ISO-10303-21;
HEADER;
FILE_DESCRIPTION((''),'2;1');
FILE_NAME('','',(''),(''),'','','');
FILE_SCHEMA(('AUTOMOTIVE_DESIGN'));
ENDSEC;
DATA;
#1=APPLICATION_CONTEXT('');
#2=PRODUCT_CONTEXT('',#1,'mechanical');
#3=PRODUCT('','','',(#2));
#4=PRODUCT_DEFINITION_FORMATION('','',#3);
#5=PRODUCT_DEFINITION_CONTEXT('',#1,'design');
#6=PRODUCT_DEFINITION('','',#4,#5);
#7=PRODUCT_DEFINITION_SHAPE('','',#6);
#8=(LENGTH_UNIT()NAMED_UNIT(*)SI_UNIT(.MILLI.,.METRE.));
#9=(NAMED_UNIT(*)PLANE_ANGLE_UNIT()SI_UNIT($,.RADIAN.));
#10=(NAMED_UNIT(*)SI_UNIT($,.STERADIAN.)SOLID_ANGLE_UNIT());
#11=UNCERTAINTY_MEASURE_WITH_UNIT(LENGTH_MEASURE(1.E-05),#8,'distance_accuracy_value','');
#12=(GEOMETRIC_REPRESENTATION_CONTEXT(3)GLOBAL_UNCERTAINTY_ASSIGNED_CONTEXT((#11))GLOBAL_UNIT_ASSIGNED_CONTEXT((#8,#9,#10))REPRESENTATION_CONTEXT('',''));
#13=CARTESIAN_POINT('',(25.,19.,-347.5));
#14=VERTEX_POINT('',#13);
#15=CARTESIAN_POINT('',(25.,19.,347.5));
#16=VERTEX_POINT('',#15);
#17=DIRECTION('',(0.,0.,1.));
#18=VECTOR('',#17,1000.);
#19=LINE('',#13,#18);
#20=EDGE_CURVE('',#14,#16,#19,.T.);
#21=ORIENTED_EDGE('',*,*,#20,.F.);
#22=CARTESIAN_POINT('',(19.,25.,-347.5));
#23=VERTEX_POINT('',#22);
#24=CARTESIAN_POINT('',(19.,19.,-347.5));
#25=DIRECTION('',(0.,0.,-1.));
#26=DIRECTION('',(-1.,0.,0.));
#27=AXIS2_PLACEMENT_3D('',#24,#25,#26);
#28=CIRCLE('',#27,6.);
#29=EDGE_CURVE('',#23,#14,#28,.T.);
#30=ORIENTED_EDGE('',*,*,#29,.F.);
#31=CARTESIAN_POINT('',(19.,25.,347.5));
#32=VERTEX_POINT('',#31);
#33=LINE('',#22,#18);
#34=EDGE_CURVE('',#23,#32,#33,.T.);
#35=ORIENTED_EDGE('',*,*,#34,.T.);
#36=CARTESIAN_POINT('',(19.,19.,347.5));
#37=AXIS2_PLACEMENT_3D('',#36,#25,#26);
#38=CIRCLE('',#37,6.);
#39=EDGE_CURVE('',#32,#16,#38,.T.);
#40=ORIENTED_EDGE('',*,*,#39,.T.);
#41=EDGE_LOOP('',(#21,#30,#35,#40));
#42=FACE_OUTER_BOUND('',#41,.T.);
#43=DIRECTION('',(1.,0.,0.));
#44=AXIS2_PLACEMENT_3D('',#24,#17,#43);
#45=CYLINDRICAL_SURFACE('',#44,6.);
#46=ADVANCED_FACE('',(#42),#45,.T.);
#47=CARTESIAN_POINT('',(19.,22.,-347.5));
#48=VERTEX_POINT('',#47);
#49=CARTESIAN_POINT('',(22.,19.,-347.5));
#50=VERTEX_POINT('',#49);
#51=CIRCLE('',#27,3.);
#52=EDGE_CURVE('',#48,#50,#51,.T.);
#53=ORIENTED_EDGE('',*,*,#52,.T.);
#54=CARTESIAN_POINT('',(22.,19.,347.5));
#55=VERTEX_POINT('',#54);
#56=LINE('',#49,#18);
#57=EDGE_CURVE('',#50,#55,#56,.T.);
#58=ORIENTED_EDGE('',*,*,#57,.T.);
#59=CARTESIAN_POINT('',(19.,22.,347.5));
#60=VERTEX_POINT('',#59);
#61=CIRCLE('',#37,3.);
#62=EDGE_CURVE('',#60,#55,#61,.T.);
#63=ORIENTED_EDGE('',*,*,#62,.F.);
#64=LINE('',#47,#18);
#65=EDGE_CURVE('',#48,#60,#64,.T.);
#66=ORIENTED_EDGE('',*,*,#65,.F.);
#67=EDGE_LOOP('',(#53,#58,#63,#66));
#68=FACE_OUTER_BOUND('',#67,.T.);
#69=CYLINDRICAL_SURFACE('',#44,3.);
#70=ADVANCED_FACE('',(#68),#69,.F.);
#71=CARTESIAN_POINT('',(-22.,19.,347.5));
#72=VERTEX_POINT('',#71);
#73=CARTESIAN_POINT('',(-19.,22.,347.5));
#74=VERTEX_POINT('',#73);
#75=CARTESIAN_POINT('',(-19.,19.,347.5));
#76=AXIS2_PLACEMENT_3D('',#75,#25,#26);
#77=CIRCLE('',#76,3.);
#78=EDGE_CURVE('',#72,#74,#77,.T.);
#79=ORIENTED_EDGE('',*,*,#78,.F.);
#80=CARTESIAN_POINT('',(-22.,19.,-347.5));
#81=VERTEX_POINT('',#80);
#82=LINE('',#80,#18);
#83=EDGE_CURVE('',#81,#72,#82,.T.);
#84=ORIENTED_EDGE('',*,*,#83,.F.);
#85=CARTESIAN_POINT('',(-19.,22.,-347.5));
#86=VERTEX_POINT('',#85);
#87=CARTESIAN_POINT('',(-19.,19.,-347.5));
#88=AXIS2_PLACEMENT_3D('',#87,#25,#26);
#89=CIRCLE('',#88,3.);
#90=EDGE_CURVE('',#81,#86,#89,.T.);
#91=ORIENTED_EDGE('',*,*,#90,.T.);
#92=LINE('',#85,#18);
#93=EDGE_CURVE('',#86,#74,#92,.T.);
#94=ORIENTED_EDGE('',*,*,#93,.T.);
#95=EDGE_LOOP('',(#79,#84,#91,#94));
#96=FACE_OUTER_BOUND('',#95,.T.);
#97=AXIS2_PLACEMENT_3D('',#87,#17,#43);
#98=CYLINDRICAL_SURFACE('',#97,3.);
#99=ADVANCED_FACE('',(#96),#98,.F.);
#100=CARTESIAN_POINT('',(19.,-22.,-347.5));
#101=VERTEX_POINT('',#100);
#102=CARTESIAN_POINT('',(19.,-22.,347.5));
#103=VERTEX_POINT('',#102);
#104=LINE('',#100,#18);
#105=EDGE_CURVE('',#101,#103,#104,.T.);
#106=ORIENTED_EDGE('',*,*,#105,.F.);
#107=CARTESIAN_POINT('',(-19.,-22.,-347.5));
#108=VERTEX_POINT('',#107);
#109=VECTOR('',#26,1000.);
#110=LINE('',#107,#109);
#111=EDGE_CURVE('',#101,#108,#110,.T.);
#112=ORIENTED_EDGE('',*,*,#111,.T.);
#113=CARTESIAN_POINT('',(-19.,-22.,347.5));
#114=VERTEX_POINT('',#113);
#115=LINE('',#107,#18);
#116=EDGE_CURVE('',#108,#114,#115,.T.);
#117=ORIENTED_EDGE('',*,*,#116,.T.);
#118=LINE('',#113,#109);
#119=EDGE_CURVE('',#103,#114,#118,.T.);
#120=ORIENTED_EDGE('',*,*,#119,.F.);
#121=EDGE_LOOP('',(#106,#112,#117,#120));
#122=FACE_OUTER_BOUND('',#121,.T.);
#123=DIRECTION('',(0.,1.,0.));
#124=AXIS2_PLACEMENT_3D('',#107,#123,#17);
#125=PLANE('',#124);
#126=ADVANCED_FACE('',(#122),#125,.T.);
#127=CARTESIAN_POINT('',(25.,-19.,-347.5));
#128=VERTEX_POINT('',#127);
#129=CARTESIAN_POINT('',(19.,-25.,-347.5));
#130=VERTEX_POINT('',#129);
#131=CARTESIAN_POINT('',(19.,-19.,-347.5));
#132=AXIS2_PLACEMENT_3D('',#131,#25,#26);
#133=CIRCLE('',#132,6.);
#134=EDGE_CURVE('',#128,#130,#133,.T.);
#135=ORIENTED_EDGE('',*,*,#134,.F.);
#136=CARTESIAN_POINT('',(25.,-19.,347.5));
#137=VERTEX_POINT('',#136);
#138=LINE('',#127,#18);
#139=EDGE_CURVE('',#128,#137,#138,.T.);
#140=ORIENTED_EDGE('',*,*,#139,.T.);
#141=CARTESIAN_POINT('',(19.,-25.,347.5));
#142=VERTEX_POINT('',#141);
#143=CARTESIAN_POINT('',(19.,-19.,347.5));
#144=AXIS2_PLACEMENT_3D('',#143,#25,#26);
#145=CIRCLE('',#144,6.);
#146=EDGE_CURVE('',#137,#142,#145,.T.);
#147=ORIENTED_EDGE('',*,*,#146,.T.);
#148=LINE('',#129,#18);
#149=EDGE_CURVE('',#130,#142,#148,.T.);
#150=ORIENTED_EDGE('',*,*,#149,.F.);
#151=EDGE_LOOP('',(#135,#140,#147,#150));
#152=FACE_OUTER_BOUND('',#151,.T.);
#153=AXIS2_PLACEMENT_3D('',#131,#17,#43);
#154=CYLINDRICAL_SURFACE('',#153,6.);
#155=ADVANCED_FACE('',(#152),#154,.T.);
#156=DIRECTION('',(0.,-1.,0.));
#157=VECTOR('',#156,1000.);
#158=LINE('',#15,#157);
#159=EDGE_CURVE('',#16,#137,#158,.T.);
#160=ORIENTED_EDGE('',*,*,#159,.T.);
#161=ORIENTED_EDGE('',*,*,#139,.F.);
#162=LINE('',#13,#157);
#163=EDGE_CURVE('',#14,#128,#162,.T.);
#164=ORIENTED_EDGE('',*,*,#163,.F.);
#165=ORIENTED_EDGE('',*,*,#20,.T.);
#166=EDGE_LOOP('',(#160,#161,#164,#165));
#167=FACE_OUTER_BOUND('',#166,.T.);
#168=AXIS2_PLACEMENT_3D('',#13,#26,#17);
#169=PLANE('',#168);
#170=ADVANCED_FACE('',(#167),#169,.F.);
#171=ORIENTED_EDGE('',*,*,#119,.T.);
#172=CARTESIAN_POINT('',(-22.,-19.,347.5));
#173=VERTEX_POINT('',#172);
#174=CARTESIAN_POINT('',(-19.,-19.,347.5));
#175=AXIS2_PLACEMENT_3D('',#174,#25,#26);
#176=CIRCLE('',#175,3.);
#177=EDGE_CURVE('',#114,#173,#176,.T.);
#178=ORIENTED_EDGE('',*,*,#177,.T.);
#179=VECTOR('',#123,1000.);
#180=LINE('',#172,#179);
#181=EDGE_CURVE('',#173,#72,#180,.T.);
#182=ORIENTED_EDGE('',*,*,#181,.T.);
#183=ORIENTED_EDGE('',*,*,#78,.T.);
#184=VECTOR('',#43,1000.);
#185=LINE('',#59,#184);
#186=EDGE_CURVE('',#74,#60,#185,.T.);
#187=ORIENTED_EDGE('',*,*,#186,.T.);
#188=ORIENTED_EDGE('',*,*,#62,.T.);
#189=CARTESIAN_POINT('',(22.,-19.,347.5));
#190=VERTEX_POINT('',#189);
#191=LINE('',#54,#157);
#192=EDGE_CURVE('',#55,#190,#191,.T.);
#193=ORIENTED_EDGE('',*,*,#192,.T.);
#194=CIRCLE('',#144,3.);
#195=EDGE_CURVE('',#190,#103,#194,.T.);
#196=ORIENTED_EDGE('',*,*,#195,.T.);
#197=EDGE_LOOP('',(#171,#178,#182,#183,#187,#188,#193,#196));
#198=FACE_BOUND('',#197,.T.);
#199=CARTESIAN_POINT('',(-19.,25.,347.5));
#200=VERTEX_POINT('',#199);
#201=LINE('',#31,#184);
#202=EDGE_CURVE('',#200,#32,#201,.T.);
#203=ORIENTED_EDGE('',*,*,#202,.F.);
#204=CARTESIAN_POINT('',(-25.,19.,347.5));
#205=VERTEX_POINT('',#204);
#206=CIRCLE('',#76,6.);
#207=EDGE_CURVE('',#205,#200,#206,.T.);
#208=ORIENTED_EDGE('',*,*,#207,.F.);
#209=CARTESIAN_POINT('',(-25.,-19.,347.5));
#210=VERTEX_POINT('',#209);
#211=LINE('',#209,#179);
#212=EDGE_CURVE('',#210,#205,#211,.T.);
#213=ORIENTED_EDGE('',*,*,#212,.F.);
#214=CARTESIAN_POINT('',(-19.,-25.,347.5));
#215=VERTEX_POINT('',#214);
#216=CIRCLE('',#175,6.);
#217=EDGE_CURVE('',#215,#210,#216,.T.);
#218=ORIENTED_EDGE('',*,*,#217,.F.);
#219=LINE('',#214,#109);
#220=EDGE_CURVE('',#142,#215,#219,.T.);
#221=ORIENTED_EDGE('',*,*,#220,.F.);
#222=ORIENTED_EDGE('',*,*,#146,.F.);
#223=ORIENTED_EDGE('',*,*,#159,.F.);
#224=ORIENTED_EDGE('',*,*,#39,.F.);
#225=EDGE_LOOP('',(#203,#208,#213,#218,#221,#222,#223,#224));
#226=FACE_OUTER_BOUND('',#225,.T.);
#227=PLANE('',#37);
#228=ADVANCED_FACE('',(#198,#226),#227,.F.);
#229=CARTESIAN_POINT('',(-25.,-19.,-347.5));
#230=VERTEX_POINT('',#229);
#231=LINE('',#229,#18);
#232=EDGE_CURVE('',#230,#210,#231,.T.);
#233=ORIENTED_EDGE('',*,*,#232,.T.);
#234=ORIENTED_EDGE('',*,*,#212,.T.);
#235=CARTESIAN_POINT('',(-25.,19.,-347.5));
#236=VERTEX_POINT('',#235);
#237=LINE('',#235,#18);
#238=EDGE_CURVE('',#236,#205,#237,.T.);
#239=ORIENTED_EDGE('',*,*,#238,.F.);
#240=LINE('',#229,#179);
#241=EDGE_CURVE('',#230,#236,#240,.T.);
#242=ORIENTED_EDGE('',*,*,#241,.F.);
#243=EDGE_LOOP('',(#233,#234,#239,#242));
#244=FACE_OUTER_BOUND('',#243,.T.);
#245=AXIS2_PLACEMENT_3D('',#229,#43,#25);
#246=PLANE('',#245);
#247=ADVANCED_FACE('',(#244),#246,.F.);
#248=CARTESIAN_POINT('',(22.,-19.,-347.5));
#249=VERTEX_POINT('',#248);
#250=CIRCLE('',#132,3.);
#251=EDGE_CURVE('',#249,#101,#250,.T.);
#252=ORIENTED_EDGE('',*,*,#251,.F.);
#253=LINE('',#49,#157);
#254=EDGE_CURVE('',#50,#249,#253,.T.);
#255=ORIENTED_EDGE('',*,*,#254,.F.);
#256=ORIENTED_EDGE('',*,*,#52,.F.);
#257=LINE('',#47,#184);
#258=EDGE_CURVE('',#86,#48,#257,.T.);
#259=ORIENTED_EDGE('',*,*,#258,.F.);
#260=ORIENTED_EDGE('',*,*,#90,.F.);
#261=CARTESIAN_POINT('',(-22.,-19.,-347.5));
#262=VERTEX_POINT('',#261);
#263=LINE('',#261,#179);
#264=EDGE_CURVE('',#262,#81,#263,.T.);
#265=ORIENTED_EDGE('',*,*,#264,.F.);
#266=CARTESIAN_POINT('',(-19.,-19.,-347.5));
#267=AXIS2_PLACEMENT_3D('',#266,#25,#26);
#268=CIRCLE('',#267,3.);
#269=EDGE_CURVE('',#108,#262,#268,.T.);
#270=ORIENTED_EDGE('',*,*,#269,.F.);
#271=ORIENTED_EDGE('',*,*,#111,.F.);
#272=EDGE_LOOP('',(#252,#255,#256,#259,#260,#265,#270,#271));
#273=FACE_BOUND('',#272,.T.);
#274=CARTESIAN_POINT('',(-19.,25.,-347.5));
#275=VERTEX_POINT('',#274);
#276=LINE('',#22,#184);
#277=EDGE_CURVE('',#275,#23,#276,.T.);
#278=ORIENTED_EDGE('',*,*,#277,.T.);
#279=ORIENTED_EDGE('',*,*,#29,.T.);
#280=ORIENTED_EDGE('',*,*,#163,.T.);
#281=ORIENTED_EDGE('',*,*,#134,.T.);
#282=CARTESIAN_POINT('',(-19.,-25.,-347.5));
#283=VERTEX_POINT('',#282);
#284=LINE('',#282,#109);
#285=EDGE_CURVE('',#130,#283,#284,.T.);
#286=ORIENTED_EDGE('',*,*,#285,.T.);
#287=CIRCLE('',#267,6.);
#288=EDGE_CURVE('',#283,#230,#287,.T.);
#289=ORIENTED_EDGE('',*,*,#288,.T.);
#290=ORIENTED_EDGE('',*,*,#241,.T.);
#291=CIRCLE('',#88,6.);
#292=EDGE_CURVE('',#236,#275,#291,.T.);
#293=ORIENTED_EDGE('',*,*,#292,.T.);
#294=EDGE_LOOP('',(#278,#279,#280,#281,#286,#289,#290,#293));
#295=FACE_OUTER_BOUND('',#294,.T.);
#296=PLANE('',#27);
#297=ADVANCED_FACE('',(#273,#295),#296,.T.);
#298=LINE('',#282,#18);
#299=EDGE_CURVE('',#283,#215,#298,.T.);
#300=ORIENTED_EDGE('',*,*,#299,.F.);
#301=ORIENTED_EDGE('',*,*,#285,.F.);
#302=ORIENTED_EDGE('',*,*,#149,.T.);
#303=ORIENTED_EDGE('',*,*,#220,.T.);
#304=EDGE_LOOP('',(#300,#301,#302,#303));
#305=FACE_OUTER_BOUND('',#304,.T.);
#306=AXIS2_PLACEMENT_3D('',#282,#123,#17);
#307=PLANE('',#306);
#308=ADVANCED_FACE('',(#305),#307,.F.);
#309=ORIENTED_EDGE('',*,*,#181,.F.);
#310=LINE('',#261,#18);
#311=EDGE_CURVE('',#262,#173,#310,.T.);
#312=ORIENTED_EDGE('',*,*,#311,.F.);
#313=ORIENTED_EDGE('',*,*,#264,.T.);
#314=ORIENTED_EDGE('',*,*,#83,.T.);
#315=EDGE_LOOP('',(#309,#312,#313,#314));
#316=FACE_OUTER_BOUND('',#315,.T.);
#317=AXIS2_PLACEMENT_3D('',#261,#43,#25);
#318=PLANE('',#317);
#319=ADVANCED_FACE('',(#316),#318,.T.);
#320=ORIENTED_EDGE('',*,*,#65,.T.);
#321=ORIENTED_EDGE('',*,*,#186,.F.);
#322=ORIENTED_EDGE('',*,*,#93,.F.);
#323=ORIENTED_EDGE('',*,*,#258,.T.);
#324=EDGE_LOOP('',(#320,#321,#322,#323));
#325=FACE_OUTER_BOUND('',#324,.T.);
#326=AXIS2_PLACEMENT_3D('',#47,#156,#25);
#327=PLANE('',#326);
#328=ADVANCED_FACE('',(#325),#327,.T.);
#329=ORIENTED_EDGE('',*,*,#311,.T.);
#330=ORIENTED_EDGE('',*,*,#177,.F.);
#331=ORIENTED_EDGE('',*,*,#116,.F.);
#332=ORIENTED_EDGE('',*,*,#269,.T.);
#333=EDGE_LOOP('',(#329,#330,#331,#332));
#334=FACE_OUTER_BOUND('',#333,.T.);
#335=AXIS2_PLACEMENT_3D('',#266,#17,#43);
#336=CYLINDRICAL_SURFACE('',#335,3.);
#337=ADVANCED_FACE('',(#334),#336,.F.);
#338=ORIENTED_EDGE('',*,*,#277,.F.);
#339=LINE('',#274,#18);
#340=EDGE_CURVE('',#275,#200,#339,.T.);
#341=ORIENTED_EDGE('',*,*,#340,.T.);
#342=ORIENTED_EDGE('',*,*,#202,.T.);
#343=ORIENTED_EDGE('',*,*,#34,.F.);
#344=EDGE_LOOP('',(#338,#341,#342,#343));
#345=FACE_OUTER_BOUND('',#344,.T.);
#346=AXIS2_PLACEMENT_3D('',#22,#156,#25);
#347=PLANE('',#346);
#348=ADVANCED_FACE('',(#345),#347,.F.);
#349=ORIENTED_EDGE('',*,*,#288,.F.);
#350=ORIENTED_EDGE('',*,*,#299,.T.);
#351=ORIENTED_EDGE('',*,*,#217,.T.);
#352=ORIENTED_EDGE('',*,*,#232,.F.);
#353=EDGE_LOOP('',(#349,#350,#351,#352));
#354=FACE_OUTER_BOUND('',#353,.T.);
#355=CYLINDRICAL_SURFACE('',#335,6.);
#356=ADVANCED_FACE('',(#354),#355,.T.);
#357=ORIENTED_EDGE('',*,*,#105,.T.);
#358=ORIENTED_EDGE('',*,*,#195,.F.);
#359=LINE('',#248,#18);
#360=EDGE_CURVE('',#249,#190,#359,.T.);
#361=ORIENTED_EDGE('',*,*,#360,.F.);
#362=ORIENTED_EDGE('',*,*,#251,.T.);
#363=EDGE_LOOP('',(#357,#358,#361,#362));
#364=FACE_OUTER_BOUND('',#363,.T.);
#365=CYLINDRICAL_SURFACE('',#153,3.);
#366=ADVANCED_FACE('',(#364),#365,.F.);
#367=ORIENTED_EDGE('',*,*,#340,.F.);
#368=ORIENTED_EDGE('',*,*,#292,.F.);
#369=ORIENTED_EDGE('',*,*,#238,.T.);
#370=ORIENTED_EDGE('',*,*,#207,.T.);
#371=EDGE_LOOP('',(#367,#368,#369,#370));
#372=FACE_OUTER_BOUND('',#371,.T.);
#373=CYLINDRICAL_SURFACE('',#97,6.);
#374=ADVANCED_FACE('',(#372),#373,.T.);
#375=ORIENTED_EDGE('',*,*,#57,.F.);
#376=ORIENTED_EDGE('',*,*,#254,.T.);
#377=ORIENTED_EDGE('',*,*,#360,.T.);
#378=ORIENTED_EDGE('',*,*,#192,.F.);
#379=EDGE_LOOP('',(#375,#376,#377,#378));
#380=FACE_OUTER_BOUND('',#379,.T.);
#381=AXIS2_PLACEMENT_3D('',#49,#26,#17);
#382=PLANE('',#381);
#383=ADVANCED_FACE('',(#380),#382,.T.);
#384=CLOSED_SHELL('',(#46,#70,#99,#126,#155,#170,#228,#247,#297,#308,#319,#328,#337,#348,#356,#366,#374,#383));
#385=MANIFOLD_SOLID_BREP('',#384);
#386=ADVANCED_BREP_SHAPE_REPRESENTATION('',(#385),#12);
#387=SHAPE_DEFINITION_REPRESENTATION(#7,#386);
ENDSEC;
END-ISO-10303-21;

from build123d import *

# Parameters (mm, degrees)
GB_6728_1986_050_X_50_X_3_1_DEPTH = 695


with BuildPart() as part:
    # Sketch1 → Gb／6728-1986方形空心型钢 050 X 50 X 3(1) (new body)
    with BuildSketch(Plane.YX.offset(-347.5)):
        with BuildLine():
            Line((-19, -25), (19, -25))
            ThreePointArc((19, -25), (23.242640687, -23.242640687), (25, -19))
            Line((25, -19), (25, 19))
            ThreePointArc((25, 19), (23.242640687, 23.242640687), (19, 25))
            Line((19, 25), (-19, 25))
            ThreePointArc((-19, 25), (-23.242640687, 23.242640687), (-25, 19))
            Line((-25, 19), (-25, -19))
            ThreePointArc((-25, -19), (-23.242640687, -23.242640687), (-19, -25))
        make_face()
        with BuildLine():
            Line((-19, -22), (19, -22))
            ThreePointArc((19, -22), (21.121320344, -21.121320344), (22, -19))
            Line((22, -19), (22, 19))
            ThreePointArc((22, 19), (21.121320344, 21.121320344), (19, 22))
            Line((19, 22), (-19, 22))
            ThreePointArc((-19, 22), (-21.121320344, 21.121320344), (-22, 19))
            Line((-22, 19), (-22, -19))
            ThreePointArc((-22, -19), (-21.121320344, -21.121320344), (-19, -22))
        make_face(mode=Mode.SUBTRACT)
    extrude(amount=GB_6728_1986_050_X_50_X_3_1_DEPTH)


solid = part.part
